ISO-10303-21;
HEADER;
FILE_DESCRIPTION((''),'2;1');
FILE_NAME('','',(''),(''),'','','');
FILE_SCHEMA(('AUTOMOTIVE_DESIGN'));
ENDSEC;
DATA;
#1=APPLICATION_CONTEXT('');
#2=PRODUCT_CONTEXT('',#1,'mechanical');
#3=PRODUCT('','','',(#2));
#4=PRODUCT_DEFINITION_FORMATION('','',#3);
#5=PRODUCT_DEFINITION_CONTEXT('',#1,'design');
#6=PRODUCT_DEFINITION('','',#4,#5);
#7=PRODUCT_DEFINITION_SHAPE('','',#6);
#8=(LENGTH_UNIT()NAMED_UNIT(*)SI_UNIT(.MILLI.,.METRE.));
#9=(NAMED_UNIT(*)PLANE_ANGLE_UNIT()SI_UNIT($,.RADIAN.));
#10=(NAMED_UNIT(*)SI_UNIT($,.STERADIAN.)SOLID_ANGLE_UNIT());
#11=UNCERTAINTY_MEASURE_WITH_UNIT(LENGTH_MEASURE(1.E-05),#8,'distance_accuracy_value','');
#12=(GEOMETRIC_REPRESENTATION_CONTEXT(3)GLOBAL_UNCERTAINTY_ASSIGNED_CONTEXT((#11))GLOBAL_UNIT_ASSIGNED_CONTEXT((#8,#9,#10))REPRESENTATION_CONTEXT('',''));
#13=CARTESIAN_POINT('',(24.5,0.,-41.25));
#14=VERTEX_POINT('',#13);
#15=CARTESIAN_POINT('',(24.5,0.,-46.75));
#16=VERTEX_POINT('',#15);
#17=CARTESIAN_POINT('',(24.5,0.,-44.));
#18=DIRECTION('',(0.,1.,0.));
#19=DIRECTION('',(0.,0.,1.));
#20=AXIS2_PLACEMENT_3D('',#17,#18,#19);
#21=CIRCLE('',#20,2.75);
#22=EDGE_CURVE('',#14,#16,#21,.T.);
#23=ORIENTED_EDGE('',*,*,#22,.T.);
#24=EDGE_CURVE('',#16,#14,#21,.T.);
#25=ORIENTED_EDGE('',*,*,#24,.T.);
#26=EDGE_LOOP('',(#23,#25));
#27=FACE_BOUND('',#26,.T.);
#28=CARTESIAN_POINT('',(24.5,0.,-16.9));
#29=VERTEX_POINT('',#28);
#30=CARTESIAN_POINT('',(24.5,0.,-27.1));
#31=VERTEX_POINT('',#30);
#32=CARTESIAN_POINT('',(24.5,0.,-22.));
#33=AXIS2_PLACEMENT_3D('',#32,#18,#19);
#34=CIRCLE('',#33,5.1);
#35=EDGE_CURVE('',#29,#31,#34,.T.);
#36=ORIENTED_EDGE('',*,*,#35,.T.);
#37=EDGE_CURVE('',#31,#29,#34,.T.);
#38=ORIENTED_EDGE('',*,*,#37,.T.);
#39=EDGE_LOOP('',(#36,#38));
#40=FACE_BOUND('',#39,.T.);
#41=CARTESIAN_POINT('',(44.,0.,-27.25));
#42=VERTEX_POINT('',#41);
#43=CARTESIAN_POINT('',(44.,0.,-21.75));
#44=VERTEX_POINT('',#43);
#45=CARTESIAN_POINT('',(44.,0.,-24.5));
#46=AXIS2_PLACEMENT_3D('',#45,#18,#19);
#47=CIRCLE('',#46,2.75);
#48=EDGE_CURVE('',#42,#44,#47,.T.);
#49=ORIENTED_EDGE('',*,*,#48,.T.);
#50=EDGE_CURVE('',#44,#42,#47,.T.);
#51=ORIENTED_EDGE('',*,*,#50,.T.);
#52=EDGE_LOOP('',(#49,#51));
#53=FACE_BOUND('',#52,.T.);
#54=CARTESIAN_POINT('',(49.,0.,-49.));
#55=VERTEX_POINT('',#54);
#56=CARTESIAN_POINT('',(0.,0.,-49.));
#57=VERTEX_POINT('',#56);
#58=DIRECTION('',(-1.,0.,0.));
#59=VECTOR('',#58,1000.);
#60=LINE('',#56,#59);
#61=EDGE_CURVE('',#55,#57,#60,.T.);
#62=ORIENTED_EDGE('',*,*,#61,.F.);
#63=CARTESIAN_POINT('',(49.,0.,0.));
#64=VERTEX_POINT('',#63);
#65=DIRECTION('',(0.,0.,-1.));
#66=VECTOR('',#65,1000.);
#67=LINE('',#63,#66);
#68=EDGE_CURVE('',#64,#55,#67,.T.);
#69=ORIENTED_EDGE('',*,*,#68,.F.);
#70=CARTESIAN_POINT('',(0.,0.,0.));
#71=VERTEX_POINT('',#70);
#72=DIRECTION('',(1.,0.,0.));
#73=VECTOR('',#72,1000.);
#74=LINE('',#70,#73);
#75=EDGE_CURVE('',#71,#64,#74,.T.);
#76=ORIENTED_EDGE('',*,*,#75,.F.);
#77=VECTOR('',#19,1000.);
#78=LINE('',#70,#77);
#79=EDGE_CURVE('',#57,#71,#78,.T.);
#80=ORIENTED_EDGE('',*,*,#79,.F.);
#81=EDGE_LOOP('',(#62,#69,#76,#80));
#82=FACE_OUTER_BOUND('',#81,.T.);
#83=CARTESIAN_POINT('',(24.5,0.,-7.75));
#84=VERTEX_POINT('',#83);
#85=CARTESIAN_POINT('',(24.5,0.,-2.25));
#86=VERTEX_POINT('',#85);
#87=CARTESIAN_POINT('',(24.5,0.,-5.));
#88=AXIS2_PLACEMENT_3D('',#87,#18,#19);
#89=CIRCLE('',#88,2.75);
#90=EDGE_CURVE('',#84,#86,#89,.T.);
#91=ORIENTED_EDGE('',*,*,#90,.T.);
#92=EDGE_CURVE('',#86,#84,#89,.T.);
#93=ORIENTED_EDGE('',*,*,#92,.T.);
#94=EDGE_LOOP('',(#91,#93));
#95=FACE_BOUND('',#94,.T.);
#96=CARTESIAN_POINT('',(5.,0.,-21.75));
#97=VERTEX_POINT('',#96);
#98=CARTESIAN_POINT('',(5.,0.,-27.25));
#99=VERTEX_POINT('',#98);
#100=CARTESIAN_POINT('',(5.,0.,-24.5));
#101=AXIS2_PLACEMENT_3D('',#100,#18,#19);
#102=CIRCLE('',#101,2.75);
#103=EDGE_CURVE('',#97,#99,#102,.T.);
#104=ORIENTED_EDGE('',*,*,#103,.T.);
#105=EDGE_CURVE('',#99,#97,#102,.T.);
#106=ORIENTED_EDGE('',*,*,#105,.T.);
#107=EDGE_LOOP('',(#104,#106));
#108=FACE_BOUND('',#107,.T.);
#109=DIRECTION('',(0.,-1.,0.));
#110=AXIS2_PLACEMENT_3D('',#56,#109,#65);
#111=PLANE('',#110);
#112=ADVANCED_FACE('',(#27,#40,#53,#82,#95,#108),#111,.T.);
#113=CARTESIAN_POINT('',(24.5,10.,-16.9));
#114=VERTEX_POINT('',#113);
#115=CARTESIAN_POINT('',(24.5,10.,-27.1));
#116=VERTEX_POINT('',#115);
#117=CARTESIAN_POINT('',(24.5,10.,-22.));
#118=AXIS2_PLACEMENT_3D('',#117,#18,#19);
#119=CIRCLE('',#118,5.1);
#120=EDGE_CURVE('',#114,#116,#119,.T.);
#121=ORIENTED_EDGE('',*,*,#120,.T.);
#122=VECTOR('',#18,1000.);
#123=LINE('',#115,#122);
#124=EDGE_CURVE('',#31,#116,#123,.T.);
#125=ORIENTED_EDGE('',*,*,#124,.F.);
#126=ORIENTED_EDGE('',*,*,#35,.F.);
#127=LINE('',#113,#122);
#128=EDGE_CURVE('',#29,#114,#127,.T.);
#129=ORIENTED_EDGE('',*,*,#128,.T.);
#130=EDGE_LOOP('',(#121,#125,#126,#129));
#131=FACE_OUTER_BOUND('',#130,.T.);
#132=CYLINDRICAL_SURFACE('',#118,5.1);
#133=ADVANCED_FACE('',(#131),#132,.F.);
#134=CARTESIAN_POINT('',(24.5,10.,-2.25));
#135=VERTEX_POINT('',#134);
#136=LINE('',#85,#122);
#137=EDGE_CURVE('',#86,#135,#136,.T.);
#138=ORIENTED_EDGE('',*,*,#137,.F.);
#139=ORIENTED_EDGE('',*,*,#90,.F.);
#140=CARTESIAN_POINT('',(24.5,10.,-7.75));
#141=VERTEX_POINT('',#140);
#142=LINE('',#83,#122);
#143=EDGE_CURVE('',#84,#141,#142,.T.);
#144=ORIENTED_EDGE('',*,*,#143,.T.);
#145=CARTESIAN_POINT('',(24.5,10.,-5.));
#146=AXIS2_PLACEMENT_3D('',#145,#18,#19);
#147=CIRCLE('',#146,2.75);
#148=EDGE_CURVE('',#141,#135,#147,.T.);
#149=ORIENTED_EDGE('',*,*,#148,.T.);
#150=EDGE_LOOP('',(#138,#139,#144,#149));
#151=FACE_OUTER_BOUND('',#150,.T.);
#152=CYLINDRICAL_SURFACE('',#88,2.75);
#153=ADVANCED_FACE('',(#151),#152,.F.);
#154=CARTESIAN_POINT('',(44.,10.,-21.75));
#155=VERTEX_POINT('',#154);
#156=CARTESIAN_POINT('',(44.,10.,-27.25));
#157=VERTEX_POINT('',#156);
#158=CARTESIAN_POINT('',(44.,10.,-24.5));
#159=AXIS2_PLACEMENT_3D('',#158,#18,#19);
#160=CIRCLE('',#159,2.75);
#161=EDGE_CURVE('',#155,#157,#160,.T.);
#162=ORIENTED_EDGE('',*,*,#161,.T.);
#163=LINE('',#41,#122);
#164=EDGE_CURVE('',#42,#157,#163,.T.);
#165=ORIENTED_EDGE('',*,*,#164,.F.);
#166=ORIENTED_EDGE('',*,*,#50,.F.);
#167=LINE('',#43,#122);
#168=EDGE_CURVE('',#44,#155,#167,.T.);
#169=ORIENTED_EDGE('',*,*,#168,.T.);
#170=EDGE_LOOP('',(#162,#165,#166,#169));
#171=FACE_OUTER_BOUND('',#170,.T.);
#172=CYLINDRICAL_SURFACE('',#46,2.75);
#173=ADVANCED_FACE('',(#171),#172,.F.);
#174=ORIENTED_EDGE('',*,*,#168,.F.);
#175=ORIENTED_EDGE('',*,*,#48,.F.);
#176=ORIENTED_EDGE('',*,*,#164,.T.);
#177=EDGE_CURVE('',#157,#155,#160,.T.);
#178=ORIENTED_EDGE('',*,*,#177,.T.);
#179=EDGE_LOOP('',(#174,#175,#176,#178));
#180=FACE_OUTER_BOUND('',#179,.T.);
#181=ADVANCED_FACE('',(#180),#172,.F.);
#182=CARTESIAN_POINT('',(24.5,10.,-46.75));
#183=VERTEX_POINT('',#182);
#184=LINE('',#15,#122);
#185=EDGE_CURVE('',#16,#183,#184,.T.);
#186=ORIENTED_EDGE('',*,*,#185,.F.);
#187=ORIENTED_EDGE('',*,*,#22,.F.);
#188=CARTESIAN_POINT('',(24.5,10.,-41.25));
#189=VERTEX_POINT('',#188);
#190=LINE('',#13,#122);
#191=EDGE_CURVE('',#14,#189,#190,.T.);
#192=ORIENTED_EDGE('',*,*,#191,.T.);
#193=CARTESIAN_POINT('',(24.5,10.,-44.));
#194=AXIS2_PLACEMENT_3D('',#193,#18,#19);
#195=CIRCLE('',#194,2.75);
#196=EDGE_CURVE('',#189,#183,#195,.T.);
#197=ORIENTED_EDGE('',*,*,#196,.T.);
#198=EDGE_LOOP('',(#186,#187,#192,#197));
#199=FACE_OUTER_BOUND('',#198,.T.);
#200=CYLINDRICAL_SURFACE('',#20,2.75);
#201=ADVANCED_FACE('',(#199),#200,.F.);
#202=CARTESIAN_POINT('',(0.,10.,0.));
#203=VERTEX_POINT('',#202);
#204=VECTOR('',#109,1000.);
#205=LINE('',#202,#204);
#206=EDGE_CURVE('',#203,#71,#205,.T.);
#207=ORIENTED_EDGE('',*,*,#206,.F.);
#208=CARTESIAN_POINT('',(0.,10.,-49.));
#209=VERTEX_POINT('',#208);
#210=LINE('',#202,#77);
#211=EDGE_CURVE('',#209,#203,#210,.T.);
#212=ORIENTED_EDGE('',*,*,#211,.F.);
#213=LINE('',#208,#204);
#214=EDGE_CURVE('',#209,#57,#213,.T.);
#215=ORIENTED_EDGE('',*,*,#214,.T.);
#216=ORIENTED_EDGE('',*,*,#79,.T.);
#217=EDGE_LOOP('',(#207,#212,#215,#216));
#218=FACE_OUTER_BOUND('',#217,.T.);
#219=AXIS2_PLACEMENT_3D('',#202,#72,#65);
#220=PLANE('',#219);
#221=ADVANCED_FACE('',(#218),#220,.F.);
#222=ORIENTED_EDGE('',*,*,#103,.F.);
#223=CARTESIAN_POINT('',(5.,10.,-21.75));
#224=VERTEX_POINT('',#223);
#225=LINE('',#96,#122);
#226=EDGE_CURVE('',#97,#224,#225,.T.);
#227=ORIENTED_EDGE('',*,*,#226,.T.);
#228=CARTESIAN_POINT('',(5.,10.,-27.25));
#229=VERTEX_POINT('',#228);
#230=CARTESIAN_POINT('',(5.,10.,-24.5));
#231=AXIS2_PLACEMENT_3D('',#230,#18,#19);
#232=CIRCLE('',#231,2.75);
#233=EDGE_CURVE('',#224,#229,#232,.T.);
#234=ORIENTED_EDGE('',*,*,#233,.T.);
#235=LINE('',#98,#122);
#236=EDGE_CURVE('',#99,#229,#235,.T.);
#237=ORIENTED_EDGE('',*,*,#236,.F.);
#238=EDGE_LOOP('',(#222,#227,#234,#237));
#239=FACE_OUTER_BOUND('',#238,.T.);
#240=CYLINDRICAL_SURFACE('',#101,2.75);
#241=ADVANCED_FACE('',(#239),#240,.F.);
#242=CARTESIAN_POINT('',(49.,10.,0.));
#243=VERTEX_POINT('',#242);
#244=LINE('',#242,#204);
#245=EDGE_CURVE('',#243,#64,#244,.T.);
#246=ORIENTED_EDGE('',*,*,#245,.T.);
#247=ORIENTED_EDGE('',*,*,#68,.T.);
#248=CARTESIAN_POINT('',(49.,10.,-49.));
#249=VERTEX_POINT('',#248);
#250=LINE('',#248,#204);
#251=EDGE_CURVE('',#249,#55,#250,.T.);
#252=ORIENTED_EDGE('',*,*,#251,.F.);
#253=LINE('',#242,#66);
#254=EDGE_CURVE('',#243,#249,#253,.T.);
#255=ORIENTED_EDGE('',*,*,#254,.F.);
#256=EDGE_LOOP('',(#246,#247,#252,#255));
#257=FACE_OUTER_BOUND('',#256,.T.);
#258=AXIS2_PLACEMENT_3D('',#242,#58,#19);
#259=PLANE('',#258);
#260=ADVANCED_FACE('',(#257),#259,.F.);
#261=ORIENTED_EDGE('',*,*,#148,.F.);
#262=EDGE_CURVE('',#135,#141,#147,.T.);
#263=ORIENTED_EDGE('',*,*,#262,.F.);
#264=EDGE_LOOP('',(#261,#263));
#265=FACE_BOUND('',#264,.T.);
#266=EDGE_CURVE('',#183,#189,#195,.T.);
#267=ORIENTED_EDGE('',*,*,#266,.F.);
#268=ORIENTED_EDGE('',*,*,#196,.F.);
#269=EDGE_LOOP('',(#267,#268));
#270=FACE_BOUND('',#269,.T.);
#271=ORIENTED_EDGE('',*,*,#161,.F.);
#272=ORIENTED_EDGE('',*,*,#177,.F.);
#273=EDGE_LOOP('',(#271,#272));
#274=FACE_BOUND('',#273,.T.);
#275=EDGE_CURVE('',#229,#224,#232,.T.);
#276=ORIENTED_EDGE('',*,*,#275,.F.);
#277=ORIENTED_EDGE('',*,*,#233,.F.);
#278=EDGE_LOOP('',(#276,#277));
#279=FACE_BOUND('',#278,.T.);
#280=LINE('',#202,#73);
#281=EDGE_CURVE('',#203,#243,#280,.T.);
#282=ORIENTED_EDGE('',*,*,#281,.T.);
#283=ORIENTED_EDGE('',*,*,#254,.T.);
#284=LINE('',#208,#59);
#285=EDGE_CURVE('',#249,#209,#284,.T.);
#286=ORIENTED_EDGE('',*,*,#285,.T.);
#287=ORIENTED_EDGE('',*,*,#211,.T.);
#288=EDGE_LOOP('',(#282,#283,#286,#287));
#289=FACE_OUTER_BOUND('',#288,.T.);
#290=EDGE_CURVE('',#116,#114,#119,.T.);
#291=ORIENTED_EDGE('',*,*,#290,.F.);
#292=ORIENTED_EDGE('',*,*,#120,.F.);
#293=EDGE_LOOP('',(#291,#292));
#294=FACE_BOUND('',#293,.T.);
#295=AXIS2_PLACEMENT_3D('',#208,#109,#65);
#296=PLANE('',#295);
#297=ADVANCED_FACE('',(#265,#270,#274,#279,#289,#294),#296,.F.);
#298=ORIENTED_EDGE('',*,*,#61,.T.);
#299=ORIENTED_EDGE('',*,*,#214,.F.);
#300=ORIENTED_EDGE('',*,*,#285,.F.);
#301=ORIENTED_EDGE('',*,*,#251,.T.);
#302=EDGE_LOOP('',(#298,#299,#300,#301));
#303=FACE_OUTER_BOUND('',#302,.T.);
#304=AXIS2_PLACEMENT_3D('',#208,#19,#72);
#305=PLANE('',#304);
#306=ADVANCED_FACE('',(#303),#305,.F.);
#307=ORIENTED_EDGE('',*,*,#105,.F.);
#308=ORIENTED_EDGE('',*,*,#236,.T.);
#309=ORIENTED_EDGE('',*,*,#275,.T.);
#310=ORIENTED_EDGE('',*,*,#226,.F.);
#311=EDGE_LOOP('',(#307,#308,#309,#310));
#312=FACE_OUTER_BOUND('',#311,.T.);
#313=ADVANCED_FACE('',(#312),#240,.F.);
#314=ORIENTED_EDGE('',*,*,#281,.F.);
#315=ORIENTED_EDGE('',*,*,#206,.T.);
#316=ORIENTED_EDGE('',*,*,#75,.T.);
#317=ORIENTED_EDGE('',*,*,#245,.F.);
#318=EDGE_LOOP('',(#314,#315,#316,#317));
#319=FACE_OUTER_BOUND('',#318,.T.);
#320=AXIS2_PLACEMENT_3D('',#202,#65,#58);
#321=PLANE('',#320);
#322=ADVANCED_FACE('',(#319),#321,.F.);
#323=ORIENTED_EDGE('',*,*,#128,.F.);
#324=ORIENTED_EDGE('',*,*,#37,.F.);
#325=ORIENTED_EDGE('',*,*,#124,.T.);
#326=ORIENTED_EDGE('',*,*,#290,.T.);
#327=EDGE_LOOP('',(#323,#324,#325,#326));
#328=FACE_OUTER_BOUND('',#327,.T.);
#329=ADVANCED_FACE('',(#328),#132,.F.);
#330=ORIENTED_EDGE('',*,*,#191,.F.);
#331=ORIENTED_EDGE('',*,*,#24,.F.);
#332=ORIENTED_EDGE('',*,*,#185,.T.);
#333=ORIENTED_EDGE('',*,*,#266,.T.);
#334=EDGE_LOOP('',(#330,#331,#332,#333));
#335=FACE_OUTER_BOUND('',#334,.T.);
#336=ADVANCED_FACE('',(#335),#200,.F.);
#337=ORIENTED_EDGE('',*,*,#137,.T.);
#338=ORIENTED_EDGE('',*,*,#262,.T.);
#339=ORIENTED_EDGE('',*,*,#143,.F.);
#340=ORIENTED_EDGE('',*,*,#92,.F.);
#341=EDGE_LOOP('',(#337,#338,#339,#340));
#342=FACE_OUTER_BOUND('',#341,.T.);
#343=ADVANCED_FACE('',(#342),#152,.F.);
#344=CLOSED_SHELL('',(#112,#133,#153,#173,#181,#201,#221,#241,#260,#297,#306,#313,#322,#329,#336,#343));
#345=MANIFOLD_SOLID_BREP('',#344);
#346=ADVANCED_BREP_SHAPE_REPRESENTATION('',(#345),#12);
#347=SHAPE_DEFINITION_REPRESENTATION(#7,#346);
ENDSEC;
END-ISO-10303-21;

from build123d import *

# Parameters (mm, degrees)
SKETCH_1_W          = 49
SKETCH_1_H          = 49
EXTRUDE_1_DEPTH     = 10
SKETCH_2_R          = 2.75
CUT_EXTRUDE_1_DEPTH = 71.014284257
HOLE_WIZARD_M12_1_D = 10.2


with BuildPart() as part:
    # 草图1 → 拉伸1 (new body)
    with BuildSketch(Plane(origin=(0, 0, 0), x_dir=(1, 0, 0), z_dir=(0, 1, 0))):
        with Locations((24.5, 24.5)):
            Rectangle(SKETCH_1_W, SKETCH_1_H)
    extrude(amount=EXTRUDE_1_DEPTH)

    # 草图2 → 切除-拉伸1 (cut, through all)
    with BuildSketch(Plane(origin=(0, 10, 0), x_dir=(-1, 0, 0), z_dir=(0, 1, 0))):
        with Locations(Location((-24.5, -5, 0), (0, 0, 90))):
            Circle(SKETCH_2_R)
        with Locations(Location((-44, -24.5, 0), (0, 0, 90))):
            Circle(SKETCH_2_R)
        with Locations(Location((-24.5, -44, 0), (0, 0, 90))):
            Circle(SKETCH_2_R)
        with Locations(Location((-5, -24.5, 0), (0, 0, 90))):
            Circle(SKETCH_2_R)
    extrude(amount=-CUT_EXTRUDE_1_DEPTH, mode=Mode.SUBTRACT)

    # M12 螺纹孔1 (through all)
    with Locations(Plane(origin=(24.5, 10, -22), x_dir=(0, 0, 1), z_dir=(0, 1, 0))):
        with Locations((0, 0)):
            Hole(HOLE_WIZARD_M12_1_D / 2)


solid = part.part
